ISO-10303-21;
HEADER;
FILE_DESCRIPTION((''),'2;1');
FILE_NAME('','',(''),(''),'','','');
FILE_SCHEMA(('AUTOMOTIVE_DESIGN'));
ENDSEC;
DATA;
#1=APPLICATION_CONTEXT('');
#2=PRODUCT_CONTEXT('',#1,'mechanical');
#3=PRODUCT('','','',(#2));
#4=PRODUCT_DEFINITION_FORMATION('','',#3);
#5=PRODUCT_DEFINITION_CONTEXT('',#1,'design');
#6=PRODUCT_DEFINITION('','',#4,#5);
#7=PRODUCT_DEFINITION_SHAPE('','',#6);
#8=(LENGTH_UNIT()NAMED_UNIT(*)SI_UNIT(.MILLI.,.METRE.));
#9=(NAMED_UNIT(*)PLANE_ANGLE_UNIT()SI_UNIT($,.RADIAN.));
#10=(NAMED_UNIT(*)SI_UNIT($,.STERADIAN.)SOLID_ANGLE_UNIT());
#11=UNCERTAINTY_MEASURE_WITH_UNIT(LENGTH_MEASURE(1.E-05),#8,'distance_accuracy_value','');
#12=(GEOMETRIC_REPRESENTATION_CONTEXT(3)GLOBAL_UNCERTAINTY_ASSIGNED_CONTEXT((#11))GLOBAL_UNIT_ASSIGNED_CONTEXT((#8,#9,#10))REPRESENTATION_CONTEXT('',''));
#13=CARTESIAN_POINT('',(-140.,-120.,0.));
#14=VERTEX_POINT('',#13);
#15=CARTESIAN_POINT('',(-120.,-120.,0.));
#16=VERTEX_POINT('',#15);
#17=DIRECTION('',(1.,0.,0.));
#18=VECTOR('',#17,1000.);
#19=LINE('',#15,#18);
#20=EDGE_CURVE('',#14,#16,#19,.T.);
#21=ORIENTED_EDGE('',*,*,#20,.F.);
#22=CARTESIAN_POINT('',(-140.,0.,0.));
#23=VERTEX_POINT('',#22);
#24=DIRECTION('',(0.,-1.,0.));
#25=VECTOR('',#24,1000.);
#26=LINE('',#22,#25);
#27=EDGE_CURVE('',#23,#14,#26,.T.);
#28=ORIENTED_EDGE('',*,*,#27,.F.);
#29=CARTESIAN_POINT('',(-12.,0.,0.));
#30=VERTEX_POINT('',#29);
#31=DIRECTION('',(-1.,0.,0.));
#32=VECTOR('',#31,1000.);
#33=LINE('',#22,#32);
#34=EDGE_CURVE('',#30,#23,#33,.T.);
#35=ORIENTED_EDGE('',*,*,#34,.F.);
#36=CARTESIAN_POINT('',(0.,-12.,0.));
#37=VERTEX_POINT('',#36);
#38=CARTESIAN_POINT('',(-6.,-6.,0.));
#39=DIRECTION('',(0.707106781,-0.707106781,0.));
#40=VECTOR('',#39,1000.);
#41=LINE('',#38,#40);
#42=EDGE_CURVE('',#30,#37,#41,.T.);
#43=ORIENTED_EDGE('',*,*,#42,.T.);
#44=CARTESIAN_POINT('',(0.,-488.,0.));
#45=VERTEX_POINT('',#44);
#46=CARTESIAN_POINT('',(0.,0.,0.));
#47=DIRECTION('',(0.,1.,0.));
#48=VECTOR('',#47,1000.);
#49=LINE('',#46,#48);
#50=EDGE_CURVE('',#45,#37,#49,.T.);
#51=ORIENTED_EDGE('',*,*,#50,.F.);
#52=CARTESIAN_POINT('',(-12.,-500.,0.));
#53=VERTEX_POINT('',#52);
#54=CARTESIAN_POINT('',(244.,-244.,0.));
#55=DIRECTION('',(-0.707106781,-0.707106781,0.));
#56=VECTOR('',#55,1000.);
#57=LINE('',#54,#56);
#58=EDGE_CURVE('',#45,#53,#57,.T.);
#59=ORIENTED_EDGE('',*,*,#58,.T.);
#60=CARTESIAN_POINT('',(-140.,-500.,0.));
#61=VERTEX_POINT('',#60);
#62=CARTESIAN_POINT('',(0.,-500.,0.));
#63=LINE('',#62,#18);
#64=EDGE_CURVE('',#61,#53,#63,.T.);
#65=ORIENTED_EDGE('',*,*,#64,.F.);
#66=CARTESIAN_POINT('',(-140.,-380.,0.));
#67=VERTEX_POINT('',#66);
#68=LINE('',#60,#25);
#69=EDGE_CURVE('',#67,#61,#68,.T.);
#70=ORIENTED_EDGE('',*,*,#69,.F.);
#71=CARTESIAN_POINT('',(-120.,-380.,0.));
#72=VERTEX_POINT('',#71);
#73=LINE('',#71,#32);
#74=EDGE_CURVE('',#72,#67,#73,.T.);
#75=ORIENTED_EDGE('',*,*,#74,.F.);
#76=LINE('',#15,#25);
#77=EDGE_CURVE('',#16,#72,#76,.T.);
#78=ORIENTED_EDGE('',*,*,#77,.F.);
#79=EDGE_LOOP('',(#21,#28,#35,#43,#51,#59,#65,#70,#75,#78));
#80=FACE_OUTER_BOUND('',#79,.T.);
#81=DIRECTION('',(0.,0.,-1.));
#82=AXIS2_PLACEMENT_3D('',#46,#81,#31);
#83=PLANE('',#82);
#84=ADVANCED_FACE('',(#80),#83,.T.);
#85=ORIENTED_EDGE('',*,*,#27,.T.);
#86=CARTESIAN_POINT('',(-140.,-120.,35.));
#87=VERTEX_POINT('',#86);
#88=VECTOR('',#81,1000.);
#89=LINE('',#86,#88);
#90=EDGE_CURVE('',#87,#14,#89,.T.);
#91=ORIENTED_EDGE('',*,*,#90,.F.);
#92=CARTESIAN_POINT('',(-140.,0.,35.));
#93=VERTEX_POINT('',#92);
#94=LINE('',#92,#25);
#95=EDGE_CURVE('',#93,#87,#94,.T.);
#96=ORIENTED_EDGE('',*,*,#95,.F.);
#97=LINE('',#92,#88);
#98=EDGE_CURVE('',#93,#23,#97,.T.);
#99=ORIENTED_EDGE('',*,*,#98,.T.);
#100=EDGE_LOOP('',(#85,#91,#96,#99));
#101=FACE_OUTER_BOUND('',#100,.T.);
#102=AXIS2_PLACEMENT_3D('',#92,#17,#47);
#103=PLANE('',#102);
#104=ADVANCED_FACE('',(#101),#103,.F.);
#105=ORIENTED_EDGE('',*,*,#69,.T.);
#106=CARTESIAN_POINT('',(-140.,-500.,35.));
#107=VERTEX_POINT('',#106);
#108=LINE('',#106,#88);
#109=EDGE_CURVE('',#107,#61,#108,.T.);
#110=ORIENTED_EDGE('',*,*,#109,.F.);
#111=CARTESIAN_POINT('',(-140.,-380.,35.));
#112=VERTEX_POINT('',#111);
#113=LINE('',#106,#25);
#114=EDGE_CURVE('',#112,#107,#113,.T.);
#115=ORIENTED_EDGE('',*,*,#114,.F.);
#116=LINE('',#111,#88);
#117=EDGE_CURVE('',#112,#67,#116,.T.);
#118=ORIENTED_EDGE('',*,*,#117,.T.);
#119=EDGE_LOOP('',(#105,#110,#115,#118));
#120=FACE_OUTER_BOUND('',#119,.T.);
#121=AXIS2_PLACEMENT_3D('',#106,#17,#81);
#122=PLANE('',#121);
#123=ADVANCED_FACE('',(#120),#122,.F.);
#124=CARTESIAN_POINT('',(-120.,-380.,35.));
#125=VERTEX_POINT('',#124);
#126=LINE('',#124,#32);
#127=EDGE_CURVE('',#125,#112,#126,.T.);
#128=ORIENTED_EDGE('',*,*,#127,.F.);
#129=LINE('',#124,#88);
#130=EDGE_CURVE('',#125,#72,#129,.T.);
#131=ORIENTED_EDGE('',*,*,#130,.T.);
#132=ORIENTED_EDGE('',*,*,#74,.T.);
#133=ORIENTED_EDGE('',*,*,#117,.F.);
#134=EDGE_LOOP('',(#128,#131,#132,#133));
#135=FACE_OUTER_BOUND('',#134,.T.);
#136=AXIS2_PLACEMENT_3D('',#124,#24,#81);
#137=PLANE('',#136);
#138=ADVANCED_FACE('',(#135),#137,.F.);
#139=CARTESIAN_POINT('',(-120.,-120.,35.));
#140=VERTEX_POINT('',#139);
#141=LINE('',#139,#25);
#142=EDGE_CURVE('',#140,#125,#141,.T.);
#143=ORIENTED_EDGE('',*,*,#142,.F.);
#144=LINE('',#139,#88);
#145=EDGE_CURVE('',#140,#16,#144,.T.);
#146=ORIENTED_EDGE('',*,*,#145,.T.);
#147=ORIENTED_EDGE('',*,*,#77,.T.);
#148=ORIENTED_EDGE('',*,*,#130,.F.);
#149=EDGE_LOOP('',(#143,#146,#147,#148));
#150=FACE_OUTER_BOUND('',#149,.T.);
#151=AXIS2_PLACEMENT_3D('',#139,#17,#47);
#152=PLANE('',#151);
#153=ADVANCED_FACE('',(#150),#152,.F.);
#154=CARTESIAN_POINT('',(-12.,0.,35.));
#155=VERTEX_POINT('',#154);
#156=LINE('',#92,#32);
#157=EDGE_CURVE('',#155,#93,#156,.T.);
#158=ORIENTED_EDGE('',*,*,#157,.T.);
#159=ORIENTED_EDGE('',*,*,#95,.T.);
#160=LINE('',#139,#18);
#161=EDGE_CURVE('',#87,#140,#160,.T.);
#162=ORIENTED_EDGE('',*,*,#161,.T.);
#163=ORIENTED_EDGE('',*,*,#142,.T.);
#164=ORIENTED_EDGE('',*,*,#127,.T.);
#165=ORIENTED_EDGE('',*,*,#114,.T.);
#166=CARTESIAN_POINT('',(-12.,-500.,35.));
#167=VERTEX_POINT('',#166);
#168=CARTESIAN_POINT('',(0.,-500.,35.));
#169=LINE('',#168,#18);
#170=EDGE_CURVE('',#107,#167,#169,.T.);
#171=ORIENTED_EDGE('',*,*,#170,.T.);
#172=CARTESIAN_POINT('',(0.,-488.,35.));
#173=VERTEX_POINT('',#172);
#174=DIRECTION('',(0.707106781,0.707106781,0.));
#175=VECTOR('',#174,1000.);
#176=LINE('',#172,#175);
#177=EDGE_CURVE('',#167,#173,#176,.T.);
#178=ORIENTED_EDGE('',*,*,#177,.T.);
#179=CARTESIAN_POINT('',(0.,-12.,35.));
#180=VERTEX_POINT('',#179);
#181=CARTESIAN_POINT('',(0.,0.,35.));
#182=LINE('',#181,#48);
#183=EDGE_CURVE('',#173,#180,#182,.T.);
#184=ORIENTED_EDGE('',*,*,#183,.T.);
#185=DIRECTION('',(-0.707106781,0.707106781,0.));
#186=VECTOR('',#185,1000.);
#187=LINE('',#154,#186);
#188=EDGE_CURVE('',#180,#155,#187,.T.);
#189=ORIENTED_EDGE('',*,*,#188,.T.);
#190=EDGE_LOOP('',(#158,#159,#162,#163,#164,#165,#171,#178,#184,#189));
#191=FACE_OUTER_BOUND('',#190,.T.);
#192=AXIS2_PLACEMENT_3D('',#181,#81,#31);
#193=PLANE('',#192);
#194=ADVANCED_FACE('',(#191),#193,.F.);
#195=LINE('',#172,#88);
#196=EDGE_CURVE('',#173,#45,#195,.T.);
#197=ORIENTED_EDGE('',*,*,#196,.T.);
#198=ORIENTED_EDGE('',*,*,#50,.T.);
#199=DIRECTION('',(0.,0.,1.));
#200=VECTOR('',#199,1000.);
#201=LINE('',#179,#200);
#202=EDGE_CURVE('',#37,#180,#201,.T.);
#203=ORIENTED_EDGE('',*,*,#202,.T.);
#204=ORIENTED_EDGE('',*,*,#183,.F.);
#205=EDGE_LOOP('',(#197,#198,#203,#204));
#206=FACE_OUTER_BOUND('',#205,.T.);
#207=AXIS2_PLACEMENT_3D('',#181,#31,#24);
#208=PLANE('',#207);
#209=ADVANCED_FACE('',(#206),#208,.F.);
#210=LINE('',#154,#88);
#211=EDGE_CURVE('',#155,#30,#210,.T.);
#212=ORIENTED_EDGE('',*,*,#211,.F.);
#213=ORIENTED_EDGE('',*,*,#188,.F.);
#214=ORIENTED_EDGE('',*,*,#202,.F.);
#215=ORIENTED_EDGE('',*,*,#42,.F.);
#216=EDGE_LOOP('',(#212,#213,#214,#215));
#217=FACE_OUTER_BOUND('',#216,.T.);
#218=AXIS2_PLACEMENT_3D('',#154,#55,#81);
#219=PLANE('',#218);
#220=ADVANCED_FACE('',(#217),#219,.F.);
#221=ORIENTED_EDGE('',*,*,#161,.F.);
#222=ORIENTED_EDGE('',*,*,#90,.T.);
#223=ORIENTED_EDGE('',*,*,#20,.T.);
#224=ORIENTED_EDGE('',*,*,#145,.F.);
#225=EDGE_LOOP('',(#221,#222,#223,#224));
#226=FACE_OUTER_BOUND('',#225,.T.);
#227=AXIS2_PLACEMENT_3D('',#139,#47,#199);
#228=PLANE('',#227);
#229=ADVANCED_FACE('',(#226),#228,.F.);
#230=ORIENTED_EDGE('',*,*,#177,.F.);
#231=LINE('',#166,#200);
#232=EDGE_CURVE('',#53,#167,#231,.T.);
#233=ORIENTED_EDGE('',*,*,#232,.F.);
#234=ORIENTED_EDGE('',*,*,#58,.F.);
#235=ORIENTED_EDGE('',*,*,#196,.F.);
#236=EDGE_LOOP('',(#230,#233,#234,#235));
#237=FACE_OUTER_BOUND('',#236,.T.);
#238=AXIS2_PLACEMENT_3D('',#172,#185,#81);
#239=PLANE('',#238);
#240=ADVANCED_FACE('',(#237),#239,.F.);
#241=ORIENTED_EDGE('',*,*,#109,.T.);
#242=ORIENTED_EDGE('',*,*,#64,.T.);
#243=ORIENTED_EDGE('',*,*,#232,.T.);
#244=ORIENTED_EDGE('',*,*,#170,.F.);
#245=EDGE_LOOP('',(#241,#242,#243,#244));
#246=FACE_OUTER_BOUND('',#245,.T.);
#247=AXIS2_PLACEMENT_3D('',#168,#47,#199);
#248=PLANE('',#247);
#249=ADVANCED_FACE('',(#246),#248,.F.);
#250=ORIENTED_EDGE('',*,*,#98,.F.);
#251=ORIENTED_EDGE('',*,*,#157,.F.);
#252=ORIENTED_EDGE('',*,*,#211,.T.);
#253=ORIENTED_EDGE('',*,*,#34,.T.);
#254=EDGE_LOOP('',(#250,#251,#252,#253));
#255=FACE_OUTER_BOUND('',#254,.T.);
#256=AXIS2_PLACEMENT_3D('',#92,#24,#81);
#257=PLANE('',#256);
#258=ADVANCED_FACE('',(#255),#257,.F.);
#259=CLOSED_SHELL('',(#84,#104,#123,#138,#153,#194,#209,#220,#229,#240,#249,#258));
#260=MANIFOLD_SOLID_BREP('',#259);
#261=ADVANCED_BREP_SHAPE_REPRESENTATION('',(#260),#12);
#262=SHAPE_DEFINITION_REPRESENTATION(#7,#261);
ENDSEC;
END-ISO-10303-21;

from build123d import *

# Parameters (mm, degrees)
EXTRUDE_1_DEPTH = 35
CHAMFER_1_SIZE  = 12


with BuildPart() as part:
    # 草图1 → 凸台-拉伸1 (new body)
    with BuildSketch(Plane.XY):
        Polygon((-140, 0), (0, 0), (0, -500), (-140, -500), (-140, -380), (-120, -380), (-120, -120), (-140, -120), align=None)
    extrude(amount=EXTRUDE_1_DEPTH)

    # 倒角1
    chamfer_1_edges = [part.edges().sort_by_distance(p)[0] for p in [
        (0, -500, 17.5),
        (0, 0, 17.5),
    ]]
    chamfer(chamfer_1_edges, length=CHAMFER_1_SIZE)


solid = part.part
